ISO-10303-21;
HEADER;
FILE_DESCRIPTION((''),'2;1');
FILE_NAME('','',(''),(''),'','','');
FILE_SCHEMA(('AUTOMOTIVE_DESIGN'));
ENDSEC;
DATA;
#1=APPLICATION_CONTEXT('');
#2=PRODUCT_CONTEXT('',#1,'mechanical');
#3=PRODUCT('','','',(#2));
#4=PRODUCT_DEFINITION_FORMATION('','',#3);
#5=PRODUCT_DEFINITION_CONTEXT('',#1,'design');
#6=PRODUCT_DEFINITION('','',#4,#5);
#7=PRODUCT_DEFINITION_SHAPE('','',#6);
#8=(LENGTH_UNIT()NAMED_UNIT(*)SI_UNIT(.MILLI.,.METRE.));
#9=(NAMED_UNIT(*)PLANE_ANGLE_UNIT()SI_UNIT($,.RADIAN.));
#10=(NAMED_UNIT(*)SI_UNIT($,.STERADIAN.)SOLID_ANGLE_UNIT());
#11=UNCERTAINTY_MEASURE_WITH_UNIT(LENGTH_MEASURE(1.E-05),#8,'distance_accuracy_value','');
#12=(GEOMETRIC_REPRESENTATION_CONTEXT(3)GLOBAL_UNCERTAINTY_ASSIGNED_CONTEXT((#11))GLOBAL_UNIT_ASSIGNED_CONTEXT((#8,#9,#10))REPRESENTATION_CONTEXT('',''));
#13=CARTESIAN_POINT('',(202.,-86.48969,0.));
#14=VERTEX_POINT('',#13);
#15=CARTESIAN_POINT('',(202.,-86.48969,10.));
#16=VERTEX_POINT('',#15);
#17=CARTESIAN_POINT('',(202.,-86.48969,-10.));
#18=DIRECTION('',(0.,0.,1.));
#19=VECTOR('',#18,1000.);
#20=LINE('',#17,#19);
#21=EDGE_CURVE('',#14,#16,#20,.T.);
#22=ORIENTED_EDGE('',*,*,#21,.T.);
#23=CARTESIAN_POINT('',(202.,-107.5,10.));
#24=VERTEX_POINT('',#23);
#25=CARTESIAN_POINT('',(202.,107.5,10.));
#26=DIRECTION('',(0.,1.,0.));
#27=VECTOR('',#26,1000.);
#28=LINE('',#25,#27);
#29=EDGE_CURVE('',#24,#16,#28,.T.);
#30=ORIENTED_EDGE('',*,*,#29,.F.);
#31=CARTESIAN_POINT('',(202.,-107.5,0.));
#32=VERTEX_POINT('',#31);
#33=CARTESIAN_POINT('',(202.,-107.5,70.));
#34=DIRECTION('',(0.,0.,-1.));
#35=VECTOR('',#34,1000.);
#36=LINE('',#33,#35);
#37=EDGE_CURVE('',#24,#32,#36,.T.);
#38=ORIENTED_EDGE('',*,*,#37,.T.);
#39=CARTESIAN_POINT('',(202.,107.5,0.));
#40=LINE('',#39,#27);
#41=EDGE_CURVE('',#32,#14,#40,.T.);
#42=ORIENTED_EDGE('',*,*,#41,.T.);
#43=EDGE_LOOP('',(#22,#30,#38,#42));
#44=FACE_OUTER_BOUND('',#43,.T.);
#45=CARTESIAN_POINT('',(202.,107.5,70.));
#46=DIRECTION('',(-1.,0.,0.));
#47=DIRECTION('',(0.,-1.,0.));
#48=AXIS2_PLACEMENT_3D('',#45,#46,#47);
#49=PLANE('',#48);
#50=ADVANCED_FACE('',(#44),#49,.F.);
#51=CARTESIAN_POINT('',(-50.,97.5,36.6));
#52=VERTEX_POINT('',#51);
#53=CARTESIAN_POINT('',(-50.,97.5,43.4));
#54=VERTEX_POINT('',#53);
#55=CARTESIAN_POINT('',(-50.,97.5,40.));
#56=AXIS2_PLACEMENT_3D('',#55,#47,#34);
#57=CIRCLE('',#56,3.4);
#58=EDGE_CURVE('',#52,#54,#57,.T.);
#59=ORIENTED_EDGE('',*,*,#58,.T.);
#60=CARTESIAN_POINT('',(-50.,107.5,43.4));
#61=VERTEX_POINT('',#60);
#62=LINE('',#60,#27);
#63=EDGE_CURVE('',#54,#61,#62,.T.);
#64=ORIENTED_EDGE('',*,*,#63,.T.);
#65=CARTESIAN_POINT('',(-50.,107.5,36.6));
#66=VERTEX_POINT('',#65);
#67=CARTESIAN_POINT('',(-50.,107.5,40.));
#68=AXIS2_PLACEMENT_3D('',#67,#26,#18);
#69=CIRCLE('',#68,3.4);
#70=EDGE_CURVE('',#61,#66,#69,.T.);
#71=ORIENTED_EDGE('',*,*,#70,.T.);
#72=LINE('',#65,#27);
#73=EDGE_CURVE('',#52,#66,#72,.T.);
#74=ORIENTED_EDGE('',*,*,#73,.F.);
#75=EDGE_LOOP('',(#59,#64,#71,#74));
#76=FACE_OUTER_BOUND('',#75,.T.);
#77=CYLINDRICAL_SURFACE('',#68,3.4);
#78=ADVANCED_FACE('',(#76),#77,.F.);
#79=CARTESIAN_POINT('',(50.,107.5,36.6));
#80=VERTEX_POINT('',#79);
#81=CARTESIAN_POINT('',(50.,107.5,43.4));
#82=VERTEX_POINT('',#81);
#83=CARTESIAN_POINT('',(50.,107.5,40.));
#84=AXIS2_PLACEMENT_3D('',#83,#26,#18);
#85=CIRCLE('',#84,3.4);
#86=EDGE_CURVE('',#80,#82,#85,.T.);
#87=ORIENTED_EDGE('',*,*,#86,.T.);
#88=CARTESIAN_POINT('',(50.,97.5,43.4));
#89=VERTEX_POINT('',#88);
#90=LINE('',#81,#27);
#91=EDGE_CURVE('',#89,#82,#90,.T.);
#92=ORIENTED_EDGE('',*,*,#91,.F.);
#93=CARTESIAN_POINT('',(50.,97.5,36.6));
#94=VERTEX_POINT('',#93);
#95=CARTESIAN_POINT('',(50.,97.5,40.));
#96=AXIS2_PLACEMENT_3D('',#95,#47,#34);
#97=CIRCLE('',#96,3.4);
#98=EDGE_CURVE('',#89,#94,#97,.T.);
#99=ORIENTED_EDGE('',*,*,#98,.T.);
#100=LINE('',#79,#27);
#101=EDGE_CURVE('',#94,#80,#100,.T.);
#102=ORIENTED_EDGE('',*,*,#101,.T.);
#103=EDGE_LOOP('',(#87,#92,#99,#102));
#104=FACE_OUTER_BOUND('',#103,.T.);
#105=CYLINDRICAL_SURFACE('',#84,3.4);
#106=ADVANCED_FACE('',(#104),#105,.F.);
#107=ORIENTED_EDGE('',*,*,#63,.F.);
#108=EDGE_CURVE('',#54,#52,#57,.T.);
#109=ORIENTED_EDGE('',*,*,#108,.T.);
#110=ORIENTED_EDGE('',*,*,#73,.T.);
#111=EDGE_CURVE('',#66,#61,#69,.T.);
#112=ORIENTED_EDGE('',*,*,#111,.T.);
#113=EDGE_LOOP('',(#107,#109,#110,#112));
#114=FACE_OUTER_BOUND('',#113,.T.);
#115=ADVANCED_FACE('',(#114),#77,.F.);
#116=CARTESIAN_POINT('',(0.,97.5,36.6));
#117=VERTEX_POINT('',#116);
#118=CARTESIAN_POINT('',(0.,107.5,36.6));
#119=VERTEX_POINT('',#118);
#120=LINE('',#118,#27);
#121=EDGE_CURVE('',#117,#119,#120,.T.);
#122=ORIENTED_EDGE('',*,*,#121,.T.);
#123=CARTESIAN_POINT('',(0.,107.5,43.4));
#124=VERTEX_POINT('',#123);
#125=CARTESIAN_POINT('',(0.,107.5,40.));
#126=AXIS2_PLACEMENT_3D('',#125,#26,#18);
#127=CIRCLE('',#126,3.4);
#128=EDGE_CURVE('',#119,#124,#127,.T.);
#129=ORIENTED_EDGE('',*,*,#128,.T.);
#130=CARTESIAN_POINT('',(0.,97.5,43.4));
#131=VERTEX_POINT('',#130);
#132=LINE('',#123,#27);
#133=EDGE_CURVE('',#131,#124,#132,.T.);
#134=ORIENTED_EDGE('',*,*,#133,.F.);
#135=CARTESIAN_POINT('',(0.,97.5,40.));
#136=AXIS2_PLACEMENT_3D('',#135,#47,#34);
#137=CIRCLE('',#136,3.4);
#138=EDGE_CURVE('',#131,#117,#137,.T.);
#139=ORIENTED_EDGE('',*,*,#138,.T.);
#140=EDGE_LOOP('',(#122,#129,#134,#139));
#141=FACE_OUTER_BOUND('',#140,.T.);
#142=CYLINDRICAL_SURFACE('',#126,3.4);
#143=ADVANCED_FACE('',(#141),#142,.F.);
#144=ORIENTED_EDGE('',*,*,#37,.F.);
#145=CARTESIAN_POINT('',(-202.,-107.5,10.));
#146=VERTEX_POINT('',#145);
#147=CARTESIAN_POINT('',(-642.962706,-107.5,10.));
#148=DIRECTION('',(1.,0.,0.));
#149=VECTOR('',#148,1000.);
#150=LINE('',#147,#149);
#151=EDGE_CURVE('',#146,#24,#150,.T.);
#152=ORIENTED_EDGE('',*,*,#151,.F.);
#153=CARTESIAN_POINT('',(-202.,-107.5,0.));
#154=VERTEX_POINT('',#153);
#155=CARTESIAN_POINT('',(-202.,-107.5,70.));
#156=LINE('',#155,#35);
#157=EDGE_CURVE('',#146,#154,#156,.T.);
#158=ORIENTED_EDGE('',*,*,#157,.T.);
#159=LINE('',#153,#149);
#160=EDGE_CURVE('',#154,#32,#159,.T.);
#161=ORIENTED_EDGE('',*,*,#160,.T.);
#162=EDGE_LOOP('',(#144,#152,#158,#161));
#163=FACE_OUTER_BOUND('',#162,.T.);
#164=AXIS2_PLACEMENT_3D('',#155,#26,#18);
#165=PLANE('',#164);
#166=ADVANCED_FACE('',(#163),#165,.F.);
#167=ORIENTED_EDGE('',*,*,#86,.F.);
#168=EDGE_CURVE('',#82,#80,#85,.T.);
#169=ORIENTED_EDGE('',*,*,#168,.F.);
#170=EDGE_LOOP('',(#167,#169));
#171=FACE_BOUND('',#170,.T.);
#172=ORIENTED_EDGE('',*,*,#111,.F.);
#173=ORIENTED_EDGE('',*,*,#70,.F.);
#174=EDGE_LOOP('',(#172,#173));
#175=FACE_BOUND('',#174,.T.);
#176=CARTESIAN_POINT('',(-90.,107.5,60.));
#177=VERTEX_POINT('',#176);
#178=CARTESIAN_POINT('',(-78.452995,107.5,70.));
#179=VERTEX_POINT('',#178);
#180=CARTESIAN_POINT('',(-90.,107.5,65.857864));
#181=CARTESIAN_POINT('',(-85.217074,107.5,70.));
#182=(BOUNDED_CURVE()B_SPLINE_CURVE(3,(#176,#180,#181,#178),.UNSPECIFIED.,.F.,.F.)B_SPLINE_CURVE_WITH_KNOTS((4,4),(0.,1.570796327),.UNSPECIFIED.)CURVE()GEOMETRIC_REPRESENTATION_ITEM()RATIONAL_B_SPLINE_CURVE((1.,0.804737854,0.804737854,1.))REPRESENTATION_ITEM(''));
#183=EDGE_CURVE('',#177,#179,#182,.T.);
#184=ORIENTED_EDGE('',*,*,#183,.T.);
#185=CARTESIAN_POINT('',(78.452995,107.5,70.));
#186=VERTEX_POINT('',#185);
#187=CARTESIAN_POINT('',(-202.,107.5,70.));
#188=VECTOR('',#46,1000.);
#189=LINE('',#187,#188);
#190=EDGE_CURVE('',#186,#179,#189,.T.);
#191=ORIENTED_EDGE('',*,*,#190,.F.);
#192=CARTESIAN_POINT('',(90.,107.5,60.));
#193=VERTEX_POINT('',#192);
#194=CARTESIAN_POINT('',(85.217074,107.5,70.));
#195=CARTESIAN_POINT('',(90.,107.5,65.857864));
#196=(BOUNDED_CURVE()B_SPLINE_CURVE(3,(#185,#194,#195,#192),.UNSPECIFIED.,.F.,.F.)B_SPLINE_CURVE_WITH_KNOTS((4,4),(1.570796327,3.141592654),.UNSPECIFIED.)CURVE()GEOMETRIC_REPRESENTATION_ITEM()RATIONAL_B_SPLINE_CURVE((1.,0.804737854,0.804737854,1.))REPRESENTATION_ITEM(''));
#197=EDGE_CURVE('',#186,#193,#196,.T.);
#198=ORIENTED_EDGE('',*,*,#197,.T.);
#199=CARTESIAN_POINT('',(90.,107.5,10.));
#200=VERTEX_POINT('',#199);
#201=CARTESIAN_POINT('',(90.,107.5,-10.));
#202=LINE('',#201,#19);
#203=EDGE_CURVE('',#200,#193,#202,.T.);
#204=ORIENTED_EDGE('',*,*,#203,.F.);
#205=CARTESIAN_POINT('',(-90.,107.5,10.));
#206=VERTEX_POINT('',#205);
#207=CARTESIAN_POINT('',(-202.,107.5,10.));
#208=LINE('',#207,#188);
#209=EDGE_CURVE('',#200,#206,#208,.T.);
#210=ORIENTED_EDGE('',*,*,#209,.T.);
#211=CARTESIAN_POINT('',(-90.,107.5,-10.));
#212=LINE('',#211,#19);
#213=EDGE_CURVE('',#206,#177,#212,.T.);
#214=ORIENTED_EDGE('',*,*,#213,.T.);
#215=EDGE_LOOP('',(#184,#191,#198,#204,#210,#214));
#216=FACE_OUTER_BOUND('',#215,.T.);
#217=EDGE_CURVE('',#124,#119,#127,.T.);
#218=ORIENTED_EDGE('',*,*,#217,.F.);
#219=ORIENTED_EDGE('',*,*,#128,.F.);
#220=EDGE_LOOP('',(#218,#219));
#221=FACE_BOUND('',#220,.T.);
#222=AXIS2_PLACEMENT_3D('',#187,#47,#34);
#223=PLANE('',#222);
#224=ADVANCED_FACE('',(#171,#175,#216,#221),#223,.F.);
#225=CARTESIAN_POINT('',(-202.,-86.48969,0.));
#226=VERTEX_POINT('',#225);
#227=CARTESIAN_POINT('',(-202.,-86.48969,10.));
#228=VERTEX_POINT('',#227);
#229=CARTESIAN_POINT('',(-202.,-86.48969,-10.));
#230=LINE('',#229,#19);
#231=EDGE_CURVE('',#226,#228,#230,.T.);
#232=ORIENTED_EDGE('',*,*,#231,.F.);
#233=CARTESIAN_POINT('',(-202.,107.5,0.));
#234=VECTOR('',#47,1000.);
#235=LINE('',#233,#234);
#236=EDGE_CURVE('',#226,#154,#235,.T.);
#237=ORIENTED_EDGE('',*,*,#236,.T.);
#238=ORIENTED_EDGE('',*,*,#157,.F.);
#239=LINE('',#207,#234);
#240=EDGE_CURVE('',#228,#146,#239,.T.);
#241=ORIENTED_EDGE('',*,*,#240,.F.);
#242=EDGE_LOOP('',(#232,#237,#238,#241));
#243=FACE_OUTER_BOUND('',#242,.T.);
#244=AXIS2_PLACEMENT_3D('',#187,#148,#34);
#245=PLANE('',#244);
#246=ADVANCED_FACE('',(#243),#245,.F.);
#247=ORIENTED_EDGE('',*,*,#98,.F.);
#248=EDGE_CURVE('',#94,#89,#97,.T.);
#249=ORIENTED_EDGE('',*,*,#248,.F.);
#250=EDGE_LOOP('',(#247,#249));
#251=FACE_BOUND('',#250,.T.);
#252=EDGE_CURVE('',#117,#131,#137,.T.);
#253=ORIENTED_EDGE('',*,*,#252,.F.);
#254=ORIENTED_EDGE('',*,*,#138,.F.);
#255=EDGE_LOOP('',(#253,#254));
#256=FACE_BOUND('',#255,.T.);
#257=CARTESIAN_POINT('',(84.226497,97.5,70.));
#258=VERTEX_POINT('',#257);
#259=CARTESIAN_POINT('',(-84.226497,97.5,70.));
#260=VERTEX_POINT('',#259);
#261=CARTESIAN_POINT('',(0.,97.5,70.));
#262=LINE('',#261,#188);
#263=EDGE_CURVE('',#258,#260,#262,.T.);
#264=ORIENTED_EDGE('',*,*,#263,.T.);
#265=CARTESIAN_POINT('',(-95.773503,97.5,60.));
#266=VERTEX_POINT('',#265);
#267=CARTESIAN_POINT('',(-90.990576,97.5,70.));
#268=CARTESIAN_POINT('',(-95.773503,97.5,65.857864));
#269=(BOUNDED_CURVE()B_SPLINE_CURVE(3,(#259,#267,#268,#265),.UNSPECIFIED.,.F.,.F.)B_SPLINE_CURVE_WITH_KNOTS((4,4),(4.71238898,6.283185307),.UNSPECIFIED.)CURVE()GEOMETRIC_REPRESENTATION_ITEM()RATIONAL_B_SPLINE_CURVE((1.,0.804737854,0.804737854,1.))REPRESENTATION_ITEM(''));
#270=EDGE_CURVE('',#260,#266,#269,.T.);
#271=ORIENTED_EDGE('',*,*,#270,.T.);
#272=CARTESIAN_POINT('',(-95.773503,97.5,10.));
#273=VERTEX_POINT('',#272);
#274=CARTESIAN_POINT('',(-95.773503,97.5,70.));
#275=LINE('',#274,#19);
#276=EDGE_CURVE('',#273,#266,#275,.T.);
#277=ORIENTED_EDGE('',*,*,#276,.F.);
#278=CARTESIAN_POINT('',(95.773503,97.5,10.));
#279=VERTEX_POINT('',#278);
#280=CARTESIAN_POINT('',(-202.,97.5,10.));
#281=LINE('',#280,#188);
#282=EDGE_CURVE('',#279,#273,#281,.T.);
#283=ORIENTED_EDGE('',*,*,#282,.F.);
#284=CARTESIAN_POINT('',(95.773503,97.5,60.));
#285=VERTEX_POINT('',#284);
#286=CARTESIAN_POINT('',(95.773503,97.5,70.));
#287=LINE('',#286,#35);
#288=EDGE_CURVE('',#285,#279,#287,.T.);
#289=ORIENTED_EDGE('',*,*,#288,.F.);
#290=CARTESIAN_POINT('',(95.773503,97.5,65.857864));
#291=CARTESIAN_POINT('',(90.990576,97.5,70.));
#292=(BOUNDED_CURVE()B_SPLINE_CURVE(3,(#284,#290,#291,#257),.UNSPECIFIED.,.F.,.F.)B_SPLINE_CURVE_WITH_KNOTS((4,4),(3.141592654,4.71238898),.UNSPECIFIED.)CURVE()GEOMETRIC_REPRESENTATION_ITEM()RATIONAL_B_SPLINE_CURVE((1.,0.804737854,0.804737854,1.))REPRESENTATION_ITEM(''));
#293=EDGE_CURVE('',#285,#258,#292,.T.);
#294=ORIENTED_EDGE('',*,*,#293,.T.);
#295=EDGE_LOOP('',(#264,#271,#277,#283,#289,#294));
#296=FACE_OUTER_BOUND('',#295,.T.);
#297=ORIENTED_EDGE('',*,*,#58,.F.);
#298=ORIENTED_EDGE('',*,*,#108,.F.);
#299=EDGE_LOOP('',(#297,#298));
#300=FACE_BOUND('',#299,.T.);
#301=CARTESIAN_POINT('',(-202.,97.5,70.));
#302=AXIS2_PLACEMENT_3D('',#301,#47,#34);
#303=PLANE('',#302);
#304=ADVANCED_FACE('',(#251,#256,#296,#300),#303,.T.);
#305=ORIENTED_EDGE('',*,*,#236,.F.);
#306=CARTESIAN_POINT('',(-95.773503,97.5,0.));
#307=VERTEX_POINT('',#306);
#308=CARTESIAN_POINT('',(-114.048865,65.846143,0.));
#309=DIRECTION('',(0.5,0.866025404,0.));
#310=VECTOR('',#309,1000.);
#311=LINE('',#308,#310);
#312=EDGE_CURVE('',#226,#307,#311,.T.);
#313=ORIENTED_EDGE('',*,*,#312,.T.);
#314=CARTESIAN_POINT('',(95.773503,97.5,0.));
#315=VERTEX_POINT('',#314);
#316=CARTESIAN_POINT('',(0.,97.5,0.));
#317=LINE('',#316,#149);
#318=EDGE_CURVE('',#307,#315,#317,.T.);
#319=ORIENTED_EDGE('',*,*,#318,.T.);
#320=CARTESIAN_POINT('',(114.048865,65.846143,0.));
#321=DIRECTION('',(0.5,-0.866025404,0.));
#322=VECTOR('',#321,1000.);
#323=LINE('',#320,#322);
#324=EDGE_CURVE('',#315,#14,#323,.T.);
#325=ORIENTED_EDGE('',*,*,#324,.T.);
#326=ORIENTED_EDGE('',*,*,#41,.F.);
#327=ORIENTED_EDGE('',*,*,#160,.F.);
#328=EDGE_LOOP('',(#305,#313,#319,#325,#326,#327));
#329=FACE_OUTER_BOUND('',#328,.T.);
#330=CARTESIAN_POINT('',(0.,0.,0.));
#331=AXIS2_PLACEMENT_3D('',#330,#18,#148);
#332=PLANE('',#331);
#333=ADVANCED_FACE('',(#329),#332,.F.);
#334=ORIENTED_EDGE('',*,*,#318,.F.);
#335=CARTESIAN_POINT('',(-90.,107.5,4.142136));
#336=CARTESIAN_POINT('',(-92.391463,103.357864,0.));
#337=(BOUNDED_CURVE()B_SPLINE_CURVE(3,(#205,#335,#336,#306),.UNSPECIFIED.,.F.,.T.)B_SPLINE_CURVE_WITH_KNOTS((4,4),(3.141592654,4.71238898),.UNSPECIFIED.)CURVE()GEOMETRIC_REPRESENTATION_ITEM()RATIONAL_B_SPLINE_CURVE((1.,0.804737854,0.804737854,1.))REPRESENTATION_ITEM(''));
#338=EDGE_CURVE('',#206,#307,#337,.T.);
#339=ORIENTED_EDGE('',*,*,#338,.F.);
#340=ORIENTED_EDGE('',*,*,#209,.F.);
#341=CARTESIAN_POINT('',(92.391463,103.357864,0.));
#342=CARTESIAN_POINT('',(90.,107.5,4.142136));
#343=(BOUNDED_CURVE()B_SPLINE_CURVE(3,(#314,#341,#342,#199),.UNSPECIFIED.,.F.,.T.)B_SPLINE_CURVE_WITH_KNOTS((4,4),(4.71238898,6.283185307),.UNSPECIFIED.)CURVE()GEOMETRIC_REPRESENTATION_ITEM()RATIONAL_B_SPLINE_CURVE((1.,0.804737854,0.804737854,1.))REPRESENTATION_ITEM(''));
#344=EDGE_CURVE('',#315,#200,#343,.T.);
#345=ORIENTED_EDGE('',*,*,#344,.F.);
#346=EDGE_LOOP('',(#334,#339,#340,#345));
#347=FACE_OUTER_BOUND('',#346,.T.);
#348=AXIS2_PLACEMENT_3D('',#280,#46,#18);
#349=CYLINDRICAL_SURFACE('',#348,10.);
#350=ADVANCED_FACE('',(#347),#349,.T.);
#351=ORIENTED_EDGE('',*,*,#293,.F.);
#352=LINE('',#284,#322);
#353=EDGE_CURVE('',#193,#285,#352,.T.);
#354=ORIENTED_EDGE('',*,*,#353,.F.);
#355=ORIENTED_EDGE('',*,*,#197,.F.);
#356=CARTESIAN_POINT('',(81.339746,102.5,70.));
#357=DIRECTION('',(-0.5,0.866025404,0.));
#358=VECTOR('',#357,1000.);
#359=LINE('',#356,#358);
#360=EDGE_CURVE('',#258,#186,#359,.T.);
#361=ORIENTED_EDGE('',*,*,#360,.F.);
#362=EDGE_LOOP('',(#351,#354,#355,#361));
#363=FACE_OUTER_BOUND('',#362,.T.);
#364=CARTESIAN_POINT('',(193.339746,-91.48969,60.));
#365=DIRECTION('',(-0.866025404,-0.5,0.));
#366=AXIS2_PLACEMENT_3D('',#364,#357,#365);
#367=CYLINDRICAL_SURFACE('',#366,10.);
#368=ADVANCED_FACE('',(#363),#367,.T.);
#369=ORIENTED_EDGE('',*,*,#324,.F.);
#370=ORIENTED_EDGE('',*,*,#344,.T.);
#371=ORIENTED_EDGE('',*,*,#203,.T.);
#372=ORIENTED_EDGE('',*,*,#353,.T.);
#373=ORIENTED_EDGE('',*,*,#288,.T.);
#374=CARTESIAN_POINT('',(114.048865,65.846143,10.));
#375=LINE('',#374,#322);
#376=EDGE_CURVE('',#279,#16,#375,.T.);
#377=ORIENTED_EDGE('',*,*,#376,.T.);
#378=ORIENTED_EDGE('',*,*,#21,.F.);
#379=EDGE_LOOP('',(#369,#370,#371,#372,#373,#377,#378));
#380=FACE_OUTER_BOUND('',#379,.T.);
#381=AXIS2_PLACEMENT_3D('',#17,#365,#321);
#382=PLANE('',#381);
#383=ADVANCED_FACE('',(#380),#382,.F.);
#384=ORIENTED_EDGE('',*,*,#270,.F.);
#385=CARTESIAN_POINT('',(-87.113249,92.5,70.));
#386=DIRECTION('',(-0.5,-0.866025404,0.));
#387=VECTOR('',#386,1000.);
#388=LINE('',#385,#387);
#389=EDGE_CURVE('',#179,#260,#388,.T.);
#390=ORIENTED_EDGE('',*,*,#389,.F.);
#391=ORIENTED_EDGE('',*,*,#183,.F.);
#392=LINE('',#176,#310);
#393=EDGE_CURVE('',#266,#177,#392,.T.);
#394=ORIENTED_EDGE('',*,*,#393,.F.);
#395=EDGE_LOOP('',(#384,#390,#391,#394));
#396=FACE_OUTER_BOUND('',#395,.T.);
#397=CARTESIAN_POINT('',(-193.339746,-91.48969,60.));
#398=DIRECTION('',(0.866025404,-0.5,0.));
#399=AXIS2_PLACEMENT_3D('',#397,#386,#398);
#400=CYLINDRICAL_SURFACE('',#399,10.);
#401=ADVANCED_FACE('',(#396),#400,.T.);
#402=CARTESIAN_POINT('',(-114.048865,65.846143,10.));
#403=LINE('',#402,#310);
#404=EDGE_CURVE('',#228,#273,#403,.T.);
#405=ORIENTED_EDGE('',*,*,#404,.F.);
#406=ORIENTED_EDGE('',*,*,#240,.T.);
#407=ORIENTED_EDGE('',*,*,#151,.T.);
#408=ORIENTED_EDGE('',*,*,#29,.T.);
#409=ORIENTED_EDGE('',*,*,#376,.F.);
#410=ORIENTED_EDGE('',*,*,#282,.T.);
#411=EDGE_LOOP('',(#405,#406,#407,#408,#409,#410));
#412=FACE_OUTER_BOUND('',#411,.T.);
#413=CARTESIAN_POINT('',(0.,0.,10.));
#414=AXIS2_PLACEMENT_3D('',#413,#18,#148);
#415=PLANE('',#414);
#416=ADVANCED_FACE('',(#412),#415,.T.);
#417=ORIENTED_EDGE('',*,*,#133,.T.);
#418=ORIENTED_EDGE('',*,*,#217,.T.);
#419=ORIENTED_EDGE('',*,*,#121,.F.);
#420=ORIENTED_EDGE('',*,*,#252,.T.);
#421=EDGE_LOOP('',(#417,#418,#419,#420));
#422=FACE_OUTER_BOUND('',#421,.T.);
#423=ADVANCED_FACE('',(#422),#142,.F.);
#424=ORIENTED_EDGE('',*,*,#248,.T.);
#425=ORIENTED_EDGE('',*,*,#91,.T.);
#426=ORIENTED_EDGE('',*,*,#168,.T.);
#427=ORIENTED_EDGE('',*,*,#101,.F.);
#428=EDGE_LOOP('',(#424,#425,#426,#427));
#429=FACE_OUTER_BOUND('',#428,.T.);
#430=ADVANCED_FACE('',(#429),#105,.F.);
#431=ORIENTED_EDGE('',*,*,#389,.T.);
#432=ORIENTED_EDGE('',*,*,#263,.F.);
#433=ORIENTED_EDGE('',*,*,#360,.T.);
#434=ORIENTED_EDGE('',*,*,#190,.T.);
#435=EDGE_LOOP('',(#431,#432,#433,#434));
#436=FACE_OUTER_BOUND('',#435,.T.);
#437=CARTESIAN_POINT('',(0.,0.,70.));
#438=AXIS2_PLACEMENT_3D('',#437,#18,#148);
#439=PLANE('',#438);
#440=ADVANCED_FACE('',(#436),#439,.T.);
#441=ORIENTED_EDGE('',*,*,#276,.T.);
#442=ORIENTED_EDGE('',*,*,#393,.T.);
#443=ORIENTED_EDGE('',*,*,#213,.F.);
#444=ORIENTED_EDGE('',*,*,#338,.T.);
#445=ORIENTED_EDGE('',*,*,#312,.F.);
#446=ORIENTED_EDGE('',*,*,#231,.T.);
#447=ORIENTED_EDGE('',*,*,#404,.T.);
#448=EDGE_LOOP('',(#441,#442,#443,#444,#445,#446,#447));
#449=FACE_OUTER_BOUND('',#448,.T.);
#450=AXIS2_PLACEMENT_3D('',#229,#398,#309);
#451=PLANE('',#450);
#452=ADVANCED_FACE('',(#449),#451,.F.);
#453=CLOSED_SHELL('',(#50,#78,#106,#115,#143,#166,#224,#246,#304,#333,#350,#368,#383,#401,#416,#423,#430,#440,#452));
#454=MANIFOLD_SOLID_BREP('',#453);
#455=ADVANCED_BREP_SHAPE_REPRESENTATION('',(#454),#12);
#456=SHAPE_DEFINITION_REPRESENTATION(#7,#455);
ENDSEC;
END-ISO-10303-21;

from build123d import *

# Parameters (mm, degrees)
SKETCH_1_W             = 404
SKETCH_1_H             = 215
EXTRUDE_1_DEPTH        = 70
SHELL_1_T              = -10
CUT_EXTRUDE_1_DEPTH    = 80
SKETCH_6_W             = 881.925411548
SKETCH_6_H             = 167.715249963
CUT_EXTRUDE_2_DEPTH    = 205
HOLE_WIZARD_M8_1_D     = 6.8
HOLE_WIZARD_M8_1_DEPTH = 19.75
HOLE_WIZARD_M8_1_TIP   = 2.042926105
FILLET_1_R             = 10


with BuildPart() as part:
    # 草图1 → 凸台-拉伸1 (new body)
    with BuildSketch(Plane.XY):
        Rectangle(SKETCH_1_W, SKETCH_1_H)
    extrude(amount=EXTRUDE_1_DEPTH)

    # 抽壳1
    shell_1_openings = [part.faces().sort_by_distance(p)[0] for p in [
        (-202, 0, 35),
        (202, 0, 35),
    ]]
    offset(amount=SHELL_1_T, openings=shell_1_openings, kind=Kind.INTERSECTION)

    # 草图2 → 切除-拉伸1 (cut)
    with BuildSketch(Plane.XY.offset(70)):
        Polygon((-202, -86.489690448), (-90, 107.5), (-202, 107.5), align=None)
        Polygon((90, 107.5), (202, 107.5), (202, -86.489690448), align=None)
    extrude(amount=-CUT_EXTRUDE_1_DEPTH, mode=Mode.SUBTRACT)

    # 草图6 → 切除-拉伸2 (cut)
    with BuildSketch(Plane.XZ.offset(107.5)):
        with Locations((-202, 93.857624982)):
            Rectangle(SKETCH_6_W, SKETCH_6_H)
    extrude(amount=-CUT_EXTRUDE_2_DEPTH, mode=Mode.SUBTRACT)

    # M8 螺纹孔1
    with Locations(Plane(origin=(0, 107.5, 0), x_dir=(1, 0, 0), z_dir=(0, 1, 0))):
        with Locations((-50, -40), (0, -40), (50, -40)):
            Hole(HOLE_WIZARD_M8_1_D / 2, depth=HOLE_WIZARD_M8_1_DEPTH)
            with Locations((0, 0, -(HOLE_WIZARD_M8_1_DEPTH + HOLE_WIZARD_M8_1_TIP / 2))):  # 118° drill point
                Cone(0, HOLE_WIZARD_M8_1_D / 2, HOLE_WIZARD_M8_1_TIP, mode=Mode.SUBTRACT)

    # 圆角1
    fillet_1_edges = [part.edges().sort_by_distance(p)[0] for p in [
        (0, 107.5, 0),
        (92.886751346, 102.5, 70),
        (-92.886751346, 102.5, 70),
    ]]
    fillet(fillet_1_edges, radius=FILLET_1_R)


solid = part.part
